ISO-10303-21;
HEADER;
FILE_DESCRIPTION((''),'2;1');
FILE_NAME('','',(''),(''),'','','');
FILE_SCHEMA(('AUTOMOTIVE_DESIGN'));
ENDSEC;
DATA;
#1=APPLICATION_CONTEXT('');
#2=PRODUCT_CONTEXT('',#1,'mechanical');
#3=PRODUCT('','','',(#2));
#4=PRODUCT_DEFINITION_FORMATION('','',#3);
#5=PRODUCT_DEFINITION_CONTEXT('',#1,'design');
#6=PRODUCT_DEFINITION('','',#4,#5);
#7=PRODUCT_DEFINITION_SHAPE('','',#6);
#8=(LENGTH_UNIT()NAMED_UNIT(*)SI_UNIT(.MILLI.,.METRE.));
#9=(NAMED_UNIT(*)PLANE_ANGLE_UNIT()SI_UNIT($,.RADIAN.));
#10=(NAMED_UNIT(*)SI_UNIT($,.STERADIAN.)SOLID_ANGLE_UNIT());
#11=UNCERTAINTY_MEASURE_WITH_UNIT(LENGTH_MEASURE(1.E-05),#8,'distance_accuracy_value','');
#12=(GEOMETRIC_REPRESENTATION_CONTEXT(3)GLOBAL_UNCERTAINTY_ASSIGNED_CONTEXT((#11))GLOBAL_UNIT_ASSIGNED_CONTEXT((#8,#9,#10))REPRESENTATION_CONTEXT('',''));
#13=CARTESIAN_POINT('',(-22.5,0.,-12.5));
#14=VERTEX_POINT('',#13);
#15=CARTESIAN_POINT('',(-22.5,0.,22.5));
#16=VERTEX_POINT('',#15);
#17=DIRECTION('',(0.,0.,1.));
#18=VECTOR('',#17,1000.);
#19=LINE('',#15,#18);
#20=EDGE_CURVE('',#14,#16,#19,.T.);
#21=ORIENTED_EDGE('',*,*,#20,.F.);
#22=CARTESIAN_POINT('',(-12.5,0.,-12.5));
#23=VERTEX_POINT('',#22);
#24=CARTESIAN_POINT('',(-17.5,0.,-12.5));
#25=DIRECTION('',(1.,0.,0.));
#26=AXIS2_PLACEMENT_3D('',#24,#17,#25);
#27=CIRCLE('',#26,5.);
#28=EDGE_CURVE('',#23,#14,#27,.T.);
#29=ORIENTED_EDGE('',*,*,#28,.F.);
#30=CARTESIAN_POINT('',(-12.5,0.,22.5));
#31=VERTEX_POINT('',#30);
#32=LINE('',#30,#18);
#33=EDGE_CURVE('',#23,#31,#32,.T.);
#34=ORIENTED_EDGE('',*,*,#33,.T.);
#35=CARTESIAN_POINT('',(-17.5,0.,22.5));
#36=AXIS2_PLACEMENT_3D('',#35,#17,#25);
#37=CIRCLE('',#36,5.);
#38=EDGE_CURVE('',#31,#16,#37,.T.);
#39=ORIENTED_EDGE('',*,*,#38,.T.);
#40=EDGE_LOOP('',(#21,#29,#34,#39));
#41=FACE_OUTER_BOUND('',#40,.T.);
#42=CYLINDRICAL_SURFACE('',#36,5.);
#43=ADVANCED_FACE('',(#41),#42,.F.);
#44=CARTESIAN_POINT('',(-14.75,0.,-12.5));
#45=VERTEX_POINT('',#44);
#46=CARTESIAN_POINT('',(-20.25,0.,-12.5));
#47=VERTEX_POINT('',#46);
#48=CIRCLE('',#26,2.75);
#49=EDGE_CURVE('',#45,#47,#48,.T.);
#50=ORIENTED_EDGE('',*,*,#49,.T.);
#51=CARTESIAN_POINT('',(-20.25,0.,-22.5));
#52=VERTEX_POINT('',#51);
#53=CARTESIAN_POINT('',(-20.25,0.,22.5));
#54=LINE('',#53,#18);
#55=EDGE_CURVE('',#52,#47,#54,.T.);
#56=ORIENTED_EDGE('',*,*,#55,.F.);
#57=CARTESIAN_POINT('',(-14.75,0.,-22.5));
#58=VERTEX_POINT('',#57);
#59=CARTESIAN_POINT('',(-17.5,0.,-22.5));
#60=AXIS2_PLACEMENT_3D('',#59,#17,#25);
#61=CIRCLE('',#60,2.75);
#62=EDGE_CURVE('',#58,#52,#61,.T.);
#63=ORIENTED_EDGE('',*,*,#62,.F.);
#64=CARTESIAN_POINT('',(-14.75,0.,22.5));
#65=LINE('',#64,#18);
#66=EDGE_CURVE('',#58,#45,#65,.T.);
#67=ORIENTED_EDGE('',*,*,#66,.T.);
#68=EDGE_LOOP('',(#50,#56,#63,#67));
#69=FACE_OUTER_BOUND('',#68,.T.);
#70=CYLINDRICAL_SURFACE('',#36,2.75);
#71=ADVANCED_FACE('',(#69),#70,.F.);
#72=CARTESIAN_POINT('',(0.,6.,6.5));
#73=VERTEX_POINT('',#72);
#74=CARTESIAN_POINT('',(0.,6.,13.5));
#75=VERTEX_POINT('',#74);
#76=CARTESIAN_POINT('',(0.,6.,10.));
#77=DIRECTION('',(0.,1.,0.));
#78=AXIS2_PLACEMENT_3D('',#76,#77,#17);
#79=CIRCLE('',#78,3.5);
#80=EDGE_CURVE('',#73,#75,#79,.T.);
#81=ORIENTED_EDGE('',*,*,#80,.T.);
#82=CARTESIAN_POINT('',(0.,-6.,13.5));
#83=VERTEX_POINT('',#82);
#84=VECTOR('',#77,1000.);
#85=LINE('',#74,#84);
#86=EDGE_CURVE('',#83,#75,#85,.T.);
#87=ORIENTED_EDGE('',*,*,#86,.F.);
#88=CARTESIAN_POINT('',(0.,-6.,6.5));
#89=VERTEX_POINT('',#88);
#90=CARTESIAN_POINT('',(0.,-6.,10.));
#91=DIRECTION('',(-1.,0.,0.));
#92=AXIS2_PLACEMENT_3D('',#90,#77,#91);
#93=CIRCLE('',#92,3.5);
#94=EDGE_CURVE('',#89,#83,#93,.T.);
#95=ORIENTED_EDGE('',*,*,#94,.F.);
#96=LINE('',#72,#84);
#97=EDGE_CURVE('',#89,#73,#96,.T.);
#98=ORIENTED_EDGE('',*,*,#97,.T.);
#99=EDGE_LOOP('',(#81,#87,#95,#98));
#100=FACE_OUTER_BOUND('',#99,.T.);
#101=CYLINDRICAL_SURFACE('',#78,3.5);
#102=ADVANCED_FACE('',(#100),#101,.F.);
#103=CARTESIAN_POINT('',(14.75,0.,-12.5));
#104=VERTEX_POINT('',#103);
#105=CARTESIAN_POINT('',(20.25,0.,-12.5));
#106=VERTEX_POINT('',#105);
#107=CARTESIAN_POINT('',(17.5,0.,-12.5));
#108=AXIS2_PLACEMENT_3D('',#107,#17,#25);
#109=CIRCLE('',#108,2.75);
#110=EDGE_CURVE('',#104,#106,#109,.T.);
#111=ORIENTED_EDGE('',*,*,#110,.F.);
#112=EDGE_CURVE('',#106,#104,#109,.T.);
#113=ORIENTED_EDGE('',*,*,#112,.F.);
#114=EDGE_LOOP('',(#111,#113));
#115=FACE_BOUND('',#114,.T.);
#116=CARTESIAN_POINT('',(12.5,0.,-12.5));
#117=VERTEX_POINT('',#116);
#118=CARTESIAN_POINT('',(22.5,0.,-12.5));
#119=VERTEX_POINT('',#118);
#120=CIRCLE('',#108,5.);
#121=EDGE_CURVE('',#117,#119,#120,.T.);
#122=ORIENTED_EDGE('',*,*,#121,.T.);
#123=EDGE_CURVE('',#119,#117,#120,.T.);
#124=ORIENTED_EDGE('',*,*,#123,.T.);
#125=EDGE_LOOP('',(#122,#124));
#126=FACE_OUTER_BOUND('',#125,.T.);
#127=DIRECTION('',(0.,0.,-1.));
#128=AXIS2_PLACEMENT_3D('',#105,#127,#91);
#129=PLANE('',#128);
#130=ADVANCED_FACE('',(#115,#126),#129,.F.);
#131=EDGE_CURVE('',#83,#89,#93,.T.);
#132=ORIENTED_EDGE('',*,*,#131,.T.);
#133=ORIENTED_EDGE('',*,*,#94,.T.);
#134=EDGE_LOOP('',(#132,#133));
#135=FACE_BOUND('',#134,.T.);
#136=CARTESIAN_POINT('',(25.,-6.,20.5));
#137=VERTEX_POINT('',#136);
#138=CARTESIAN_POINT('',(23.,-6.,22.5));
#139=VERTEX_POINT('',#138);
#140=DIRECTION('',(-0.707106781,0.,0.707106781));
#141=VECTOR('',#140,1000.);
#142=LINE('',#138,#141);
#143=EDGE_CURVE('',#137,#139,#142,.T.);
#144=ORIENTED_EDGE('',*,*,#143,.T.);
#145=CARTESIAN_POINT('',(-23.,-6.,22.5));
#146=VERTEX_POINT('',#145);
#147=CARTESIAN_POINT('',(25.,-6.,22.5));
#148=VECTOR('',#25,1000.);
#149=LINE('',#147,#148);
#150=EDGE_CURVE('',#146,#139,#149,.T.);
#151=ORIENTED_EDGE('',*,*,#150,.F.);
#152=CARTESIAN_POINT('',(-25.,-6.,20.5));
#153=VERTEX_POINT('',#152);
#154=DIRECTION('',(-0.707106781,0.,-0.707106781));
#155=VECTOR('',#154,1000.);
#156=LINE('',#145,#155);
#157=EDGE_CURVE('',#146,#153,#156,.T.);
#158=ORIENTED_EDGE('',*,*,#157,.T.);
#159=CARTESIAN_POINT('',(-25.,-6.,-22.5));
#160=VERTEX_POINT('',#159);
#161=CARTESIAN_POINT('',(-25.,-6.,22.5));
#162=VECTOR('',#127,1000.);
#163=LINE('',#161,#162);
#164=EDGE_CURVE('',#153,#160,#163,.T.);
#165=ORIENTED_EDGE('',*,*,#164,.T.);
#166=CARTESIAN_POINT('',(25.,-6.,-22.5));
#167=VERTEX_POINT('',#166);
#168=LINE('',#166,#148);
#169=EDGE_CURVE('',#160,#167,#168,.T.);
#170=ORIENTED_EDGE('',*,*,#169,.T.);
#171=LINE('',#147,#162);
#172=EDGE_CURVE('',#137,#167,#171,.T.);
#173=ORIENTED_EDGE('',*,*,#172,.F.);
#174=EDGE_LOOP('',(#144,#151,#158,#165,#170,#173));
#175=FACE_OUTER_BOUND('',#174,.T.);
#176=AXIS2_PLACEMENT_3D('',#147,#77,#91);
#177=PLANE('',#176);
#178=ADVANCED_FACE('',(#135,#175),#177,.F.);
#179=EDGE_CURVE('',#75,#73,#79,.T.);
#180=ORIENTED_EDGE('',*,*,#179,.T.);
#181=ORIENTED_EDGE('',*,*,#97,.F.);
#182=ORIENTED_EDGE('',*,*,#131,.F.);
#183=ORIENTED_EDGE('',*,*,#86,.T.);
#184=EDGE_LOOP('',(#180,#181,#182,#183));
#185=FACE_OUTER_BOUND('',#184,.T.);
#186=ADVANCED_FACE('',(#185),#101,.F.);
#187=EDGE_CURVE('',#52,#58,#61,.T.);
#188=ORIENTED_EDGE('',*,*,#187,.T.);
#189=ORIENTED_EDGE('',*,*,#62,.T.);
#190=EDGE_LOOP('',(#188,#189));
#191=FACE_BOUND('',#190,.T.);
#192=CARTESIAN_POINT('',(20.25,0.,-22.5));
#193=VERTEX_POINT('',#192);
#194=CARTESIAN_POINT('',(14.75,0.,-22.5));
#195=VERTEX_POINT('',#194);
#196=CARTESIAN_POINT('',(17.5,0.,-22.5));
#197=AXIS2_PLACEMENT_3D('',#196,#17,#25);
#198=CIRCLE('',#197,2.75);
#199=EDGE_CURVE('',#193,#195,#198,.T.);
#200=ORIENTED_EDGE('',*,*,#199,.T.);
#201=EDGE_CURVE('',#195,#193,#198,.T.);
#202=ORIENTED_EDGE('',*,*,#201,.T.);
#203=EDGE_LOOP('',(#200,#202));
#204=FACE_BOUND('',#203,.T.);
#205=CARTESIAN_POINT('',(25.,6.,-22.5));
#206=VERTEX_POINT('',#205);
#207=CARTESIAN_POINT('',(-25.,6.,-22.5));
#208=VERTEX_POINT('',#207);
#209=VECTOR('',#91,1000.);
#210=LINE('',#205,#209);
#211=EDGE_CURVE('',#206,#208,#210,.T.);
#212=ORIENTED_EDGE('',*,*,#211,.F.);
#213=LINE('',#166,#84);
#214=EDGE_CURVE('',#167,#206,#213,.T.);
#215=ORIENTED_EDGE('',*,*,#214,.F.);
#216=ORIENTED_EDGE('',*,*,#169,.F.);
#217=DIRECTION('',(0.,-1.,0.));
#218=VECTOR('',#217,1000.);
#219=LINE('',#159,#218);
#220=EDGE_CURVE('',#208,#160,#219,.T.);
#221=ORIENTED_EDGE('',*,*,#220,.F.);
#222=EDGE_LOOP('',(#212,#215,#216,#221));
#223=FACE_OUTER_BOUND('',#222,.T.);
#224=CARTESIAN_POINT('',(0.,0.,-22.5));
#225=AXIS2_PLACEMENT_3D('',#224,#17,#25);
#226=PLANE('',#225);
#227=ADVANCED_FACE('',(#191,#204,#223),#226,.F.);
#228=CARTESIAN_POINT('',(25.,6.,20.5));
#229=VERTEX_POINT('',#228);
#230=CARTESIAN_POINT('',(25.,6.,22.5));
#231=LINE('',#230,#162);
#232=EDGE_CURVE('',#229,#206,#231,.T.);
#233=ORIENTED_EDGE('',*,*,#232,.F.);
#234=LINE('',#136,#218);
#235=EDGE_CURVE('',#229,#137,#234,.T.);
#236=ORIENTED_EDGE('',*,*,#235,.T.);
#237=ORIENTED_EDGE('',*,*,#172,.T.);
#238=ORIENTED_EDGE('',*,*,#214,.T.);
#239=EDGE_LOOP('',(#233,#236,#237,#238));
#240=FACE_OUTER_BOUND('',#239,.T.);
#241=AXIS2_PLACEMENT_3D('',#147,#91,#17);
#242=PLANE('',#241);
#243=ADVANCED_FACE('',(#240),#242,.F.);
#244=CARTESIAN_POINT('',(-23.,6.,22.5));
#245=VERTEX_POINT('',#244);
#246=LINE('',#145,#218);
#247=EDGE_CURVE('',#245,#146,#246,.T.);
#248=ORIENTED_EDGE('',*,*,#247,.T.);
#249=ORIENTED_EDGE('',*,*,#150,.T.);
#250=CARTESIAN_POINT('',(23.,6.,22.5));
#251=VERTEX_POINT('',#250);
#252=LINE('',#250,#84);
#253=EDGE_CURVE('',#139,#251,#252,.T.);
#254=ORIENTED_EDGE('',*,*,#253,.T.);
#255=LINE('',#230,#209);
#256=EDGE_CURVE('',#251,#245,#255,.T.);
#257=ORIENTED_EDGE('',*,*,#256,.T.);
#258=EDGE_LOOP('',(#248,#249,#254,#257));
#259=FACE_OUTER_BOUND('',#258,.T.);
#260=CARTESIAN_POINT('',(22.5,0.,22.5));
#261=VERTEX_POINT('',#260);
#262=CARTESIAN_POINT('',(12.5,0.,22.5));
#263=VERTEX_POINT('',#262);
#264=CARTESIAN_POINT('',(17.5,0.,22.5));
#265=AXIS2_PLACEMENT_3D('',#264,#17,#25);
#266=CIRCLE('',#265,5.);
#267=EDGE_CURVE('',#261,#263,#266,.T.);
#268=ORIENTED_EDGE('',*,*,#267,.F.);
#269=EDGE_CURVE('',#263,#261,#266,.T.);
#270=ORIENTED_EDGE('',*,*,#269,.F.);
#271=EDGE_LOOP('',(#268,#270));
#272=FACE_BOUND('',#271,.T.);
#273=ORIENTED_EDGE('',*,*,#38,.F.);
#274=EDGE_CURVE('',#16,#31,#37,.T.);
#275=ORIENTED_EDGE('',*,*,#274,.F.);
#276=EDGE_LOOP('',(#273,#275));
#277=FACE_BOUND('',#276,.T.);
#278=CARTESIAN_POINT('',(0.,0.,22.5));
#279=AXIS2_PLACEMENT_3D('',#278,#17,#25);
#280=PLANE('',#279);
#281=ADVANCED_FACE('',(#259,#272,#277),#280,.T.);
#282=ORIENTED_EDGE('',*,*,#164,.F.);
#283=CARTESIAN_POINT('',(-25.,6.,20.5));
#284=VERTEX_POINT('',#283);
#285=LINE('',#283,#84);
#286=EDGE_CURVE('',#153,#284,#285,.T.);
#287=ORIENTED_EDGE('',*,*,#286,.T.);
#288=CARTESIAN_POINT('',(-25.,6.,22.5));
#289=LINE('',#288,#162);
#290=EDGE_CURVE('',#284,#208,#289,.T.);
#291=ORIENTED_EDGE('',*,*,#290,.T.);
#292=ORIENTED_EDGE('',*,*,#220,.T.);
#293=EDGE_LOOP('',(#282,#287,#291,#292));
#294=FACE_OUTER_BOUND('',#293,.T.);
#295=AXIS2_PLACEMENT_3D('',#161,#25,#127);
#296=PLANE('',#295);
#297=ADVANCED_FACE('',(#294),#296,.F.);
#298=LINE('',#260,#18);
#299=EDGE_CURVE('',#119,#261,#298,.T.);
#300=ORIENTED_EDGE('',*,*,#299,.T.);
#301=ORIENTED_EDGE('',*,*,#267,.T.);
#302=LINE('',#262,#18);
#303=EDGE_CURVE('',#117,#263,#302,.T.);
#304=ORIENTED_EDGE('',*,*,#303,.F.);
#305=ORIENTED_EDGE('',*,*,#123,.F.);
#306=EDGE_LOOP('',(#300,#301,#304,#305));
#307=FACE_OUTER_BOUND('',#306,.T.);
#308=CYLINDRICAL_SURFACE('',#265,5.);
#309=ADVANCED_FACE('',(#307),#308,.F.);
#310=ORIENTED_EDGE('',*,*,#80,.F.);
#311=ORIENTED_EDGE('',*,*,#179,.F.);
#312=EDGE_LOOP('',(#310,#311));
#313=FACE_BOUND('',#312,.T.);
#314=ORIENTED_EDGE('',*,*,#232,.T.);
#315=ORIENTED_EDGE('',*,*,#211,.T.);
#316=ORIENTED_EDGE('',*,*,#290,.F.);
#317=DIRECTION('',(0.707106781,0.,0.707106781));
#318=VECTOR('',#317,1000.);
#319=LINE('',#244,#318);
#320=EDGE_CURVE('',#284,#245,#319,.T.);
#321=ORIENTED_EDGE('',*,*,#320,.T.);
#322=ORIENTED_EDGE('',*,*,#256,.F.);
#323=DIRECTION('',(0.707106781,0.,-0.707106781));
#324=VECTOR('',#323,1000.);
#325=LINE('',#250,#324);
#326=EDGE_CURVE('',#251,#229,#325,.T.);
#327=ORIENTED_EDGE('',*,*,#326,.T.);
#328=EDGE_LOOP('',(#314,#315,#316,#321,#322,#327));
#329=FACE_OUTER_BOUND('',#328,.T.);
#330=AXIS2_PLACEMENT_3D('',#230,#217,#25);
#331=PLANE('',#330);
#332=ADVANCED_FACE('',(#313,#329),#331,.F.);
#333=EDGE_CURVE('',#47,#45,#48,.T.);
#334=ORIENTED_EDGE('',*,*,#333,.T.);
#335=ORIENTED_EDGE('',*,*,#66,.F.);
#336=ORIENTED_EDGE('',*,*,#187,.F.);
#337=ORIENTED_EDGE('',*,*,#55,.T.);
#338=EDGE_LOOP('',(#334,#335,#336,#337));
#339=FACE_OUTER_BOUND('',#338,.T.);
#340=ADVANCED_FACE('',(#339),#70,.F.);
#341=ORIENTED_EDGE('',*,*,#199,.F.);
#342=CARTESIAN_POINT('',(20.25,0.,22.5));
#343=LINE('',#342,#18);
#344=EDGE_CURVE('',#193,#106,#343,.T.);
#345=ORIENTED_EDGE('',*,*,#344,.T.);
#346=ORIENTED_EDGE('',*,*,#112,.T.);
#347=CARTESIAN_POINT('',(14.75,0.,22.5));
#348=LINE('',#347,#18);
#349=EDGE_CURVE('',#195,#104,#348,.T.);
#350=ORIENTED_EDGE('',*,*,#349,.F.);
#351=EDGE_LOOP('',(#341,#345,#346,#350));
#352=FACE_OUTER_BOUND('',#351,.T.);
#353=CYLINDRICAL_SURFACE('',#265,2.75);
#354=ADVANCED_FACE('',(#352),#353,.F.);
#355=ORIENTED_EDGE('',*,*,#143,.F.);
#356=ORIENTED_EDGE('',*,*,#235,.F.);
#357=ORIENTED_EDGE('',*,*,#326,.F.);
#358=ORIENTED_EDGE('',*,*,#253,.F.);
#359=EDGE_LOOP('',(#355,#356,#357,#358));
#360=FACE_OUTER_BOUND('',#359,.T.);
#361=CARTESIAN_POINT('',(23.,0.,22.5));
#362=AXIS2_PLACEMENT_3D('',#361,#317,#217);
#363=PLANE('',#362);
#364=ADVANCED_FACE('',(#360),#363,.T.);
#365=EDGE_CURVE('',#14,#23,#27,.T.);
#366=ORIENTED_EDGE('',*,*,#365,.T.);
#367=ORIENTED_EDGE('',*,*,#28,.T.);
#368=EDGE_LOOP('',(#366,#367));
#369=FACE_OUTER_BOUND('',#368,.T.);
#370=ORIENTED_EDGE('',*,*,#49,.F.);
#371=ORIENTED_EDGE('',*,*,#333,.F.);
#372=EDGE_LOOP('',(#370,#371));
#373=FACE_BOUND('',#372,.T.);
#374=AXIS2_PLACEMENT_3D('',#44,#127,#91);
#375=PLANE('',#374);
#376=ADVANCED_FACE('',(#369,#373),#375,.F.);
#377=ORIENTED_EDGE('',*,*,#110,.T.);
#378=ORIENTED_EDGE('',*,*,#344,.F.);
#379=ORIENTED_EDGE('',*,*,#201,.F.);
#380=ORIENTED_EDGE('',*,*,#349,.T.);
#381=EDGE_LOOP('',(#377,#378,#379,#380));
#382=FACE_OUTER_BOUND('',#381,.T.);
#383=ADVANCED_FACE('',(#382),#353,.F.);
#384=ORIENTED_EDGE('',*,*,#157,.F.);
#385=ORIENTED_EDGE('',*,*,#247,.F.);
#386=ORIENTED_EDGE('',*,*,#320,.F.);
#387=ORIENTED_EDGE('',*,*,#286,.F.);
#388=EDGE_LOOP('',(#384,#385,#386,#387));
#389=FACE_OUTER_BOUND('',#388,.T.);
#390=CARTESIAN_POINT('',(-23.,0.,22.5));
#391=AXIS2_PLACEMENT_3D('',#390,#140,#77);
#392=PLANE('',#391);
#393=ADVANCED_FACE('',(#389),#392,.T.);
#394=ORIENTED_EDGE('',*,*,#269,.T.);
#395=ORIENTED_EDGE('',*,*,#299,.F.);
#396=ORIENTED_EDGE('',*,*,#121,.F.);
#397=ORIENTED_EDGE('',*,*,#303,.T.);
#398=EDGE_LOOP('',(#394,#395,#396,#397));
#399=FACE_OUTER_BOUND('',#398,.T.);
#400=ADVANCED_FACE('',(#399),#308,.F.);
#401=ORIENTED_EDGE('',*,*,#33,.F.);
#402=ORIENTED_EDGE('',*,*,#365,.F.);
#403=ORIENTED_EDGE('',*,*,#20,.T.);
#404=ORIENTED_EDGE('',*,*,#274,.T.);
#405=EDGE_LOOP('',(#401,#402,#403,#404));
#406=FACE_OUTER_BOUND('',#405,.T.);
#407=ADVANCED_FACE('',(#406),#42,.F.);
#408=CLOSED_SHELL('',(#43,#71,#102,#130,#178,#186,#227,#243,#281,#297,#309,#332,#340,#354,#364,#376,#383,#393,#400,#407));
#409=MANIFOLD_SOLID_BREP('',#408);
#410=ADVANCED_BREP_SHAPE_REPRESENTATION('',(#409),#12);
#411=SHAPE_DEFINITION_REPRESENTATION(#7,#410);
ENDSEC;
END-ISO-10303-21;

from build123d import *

# Parameters (mm, degrees)
SKETCH1_W                                    = 50
SKETCH1_H                                    = 12
BOSS_EXTRUDE1_DEPTH                          = 22.5
M8X1_0_TAPPED_HOLE1_D                        = 7
HEX_SOCKET_CAP_SCREW_HOLE_TYPE_1_D           = 5.5
HEX_SOCKET_CAP_SCREW_HOLE_TYPE_1_CBORE_D     = 10
HEX_SOCKET_CAP_SCREW_HOLE_TYPE_1_CBORE_DEPTH = 35
CHAMFER1_SIZE                                = 2


with BuildPart() as part:
    # Sketch1 → Boss-Extrude1 (new, symmetric)
    with BuildSketch(Plane.XY):
        Rectangle(SKETCH1_W, SKETCH1_H)
    extrude(amount=BOSS_EXTRUDE1_DEPTH, both=True)

    # M8x1.0 Tapped Hole1 (through all)
    with Locations(Plane(origin=(0, 6, 0), x_dir=(1, 0, 0), z_dir=(0, 1, 0))):
        with Locations((0, -10)):
            Hole(M8X1_0_TAPPED_HOLE1_D / 2)

    # Hex socket cap screw hole type 1 (through all)
    with Locations(Plane.XY.offset(22.5)):
        with Locations((-17.5, 0), (17.5, 0)):
            CounterBoreHole(HEX_SOCKET_CAP_SCREW_HOLE_TYPE_1_D / 2, HEX_SOCKET_CAP_SCREW_HOLE_TYPE_1_CBORE_D / 2, HEX_SOCKET_CAP_SCREW_HOLE_TYPE_1_CBORE_DEPTH)

    # Chamfer1
    chamfer1_edges = [part.edges().sort_by_distance(p)[0] for p in [
        (25, 0, 22.5),
        (-25, 0, 22.5),
    ]]
    chamfer(chamfer1_edges, length=CHAMFER1_SIZE)


solid = part.part
